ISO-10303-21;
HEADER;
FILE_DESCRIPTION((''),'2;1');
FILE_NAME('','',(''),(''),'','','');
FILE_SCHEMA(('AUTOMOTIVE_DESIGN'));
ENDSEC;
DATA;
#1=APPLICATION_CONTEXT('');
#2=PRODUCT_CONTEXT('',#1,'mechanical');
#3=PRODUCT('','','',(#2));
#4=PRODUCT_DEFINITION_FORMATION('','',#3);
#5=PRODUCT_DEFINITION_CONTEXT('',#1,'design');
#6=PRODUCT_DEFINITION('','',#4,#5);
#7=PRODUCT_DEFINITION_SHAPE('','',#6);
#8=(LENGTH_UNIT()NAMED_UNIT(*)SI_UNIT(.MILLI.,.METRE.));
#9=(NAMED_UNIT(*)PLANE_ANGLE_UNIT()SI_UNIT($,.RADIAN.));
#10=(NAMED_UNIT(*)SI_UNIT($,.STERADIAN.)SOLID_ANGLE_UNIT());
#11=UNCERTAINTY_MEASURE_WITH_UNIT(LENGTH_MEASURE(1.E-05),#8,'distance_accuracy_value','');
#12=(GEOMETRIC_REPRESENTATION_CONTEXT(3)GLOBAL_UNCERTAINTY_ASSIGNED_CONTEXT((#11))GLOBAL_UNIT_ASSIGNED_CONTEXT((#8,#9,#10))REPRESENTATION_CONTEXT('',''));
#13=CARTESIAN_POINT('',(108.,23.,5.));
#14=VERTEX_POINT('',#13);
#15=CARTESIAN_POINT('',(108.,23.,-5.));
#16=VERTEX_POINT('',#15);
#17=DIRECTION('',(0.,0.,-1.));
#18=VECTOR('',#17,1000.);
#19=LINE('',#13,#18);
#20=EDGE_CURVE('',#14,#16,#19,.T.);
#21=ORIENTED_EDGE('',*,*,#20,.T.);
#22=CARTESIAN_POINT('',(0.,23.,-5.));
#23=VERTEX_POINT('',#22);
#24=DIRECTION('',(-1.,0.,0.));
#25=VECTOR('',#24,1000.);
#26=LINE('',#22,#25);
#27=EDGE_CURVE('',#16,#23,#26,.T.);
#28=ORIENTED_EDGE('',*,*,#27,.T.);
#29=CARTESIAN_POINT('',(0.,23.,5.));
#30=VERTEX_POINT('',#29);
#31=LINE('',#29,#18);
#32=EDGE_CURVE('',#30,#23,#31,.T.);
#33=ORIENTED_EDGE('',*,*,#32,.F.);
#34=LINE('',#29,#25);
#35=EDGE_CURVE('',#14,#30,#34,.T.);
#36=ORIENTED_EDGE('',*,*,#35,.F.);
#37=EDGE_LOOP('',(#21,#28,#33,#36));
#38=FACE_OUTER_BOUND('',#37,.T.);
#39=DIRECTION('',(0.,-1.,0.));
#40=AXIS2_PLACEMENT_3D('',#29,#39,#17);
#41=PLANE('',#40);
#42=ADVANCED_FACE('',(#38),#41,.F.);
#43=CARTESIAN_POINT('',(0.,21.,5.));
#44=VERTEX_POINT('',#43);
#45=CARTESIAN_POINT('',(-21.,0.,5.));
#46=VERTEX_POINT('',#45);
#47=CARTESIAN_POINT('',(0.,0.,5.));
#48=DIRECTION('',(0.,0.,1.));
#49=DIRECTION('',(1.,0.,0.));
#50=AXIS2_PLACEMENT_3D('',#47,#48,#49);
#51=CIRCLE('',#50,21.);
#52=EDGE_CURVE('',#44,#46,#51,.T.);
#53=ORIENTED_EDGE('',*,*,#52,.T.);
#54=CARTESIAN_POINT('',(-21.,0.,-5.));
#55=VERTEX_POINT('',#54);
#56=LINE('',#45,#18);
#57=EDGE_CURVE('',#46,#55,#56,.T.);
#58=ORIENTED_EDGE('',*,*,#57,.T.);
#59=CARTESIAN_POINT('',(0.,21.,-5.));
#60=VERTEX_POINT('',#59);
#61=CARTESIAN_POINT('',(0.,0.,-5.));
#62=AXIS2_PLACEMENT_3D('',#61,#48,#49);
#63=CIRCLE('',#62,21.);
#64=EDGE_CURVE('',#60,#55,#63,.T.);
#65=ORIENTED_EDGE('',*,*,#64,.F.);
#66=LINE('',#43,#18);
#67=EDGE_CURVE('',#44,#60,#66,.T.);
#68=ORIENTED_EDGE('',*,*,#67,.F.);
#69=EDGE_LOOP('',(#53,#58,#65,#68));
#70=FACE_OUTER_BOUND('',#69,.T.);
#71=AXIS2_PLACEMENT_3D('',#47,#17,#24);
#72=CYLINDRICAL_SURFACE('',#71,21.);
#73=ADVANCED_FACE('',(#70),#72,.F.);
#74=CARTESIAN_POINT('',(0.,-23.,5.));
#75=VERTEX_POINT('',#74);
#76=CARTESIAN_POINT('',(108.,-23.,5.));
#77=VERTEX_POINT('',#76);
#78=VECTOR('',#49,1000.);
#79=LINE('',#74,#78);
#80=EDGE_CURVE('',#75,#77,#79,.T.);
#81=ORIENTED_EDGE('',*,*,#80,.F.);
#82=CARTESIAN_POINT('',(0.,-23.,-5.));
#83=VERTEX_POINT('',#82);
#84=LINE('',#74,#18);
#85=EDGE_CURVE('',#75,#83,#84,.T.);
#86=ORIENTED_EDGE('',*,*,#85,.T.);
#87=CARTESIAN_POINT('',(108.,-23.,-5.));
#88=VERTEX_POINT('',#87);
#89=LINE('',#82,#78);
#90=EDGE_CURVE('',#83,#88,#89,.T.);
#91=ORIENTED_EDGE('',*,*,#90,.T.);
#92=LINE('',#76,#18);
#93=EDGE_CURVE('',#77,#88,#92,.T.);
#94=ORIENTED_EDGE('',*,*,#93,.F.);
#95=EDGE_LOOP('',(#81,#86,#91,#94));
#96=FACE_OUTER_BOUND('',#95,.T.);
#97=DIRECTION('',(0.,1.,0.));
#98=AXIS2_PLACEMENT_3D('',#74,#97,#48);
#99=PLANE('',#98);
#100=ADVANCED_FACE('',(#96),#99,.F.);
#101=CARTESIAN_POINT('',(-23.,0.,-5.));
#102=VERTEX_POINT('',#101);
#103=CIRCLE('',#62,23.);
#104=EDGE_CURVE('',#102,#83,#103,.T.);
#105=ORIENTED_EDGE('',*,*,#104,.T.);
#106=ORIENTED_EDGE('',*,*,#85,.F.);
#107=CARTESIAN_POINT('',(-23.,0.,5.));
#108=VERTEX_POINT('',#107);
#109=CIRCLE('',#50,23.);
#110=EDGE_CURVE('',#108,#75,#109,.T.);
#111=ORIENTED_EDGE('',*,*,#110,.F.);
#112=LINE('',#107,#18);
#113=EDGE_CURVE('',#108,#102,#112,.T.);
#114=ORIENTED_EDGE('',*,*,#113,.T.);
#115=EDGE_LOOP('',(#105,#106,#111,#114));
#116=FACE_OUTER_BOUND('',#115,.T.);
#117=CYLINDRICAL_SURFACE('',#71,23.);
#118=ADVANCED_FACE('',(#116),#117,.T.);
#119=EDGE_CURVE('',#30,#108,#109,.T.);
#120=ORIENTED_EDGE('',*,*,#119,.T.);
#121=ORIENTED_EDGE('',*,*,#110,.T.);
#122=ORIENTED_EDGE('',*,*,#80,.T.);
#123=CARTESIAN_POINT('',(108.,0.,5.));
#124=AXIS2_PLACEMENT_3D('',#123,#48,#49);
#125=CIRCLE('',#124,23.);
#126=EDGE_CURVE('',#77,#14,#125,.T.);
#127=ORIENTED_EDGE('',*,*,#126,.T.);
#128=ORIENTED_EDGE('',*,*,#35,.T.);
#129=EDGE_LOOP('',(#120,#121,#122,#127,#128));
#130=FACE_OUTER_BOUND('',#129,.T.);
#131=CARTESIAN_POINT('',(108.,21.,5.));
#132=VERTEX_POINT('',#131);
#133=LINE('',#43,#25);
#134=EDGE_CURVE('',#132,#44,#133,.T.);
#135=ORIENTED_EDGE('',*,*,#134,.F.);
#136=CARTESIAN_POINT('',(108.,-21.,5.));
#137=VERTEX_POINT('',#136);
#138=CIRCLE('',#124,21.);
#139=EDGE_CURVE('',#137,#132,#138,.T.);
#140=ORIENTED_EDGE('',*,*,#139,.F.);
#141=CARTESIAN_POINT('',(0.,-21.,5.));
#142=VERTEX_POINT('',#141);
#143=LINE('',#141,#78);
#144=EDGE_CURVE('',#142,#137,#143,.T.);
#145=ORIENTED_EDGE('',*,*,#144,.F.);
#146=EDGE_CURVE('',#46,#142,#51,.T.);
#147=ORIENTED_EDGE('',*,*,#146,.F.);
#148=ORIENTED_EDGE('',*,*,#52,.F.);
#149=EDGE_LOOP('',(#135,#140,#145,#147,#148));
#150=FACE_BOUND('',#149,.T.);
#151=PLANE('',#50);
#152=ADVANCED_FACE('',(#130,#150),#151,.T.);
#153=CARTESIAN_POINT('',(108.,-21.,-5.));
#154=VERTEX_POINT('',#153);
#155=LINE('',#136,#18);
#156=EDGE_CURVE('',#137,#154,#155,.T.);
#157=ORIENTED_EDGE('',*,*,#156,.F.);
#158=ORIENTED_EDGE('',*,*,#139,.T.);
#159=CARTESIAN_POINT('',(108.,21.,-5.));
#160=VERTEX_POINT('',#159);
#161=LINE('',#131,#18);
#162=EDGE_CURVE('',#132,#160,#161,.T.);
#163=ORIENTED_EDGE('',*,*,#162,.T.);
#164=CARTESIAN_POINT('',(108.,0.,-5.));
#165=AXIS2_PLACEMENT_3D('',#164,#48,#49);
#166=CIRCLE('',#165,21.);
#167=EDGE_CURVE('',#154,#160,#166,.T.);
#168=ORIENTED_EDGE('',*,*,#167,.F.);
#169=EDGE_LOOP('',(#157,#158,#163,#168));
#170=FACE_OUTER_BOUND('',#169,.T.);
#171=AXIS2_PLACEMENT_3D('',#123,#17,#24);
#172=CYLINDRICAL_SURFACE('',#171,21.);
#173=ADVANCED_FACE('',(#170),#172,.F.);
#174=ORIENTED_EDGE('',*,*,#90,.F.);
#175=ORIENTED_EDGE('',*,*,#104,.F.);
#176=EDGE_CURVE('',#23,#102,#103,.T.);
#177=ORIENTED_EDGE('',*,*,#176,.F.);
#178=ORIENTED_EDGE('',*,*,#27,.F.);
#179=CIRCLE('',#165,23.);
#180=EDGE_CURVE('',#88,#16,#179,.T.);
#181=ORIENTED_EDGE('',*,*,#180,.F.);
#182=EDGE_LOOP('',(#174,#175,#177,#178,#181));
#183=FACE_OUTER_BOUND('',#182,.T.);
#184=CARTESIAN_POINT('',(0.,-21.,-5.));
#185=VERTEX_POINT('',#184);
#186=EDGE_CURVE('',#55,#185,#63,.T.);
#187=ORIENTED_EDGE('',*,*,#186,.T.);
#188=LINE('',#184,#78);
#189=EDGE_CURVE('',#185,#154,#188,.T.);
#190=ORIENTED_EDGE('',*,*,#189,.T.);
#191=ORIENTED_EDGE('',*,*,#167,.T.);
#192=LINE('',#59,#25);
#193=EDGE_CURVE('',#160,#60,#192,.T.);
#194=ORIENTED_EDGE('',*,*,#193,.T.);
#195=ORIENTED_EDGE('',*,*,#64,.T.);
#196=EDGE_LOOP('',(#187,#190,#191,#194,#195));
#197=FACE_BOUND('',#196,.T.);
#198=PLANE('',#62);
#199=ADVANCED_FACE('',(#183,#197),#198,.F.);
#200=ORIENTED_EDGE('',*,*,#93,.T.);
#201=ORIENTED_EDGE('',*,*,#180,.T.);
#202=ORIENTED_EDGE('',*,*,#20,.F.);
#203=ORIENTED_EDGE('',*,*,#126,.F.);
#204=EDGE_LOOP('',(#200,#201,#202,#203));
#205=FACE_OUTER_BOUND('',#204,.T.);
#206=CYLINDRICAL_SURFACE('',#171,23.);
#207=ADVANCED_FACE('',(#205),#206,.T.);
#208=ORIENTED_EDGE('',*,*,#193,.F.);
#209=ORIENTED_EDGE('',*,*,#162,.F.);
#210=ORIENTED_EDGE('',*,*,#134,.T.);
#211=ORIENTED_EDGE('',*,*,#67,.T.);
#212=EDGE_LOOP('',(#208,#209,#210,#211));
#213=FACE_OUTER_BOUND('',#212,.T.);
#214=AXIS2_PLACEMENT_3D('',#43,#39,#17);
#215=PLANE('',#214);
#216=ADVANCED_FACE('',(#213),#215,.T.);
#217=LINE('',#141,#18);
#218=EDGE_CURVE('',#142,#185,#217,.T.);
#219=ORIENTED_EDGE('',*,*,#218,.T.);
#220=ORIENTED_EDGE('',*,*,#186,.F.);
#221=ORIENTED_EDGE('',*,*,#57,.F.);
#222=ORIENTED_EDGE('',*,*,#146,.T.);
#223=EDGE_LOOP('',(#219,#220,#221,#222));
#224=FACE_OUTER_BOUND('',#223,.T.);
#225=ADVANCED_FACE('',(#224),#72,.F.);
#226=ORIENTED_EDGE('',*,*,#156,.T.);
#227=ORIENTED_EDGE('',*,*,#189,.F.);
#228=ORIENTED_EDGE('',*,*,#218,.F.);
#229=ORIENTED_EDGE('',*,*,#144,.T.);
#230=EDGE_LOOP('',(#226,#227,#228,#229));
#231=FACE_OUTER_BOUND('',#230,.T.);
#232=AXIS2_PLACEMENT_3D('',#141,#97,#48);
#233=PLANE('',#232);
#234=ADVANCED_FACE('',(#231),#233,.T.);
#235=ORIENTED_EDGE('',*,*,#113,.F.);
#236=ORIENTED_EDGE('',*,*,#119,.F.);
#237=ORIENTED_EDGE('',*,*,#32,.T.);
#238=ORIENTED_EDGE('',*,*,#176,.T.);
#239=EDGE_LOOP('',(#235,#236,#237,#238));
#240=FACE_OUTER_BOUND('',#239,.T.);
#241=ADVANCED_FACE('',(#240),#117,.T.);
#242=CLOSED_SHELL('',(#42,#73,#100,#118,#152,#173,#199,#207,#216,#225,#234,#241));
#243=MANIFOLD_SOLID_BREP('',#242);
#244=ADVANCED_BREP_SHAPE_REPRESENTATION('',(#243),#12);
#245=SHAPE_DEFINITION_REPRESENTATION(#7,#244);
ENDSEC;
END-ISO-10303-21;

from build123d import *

# Parameters (mm, degrees)
EXTRUDE_1_DEPTH = 5


with BuildPart() as part:
    # 草图1 → 拉伸-薄壁1 (new, symmetric)
    with BuildSketch(Plane.XY):
        with BuildLine():
            Line((108, -23), (0, -23))
            ThreePointArc((0, -23), (-23, 0), (0, 23))
            Line((0, 23), (108, 23))
            ThreePointArc((108, 23), (131, 0), (108, -23))
        make_face()
        with BuildLine():
            Line((108, -21), (0, -21))
            ThreePointArc((0, -21), (-21, 0), (0, 21))
            Line((0, 21), (108, 21))
            ThreePointArc((108, 21), (129, 0), (108, -21))
        make_face(mode=Mode.SUBTRACT)
    extrude(amount=EXTRUDE_1_DEPTH, both=True)


solid = part.part
